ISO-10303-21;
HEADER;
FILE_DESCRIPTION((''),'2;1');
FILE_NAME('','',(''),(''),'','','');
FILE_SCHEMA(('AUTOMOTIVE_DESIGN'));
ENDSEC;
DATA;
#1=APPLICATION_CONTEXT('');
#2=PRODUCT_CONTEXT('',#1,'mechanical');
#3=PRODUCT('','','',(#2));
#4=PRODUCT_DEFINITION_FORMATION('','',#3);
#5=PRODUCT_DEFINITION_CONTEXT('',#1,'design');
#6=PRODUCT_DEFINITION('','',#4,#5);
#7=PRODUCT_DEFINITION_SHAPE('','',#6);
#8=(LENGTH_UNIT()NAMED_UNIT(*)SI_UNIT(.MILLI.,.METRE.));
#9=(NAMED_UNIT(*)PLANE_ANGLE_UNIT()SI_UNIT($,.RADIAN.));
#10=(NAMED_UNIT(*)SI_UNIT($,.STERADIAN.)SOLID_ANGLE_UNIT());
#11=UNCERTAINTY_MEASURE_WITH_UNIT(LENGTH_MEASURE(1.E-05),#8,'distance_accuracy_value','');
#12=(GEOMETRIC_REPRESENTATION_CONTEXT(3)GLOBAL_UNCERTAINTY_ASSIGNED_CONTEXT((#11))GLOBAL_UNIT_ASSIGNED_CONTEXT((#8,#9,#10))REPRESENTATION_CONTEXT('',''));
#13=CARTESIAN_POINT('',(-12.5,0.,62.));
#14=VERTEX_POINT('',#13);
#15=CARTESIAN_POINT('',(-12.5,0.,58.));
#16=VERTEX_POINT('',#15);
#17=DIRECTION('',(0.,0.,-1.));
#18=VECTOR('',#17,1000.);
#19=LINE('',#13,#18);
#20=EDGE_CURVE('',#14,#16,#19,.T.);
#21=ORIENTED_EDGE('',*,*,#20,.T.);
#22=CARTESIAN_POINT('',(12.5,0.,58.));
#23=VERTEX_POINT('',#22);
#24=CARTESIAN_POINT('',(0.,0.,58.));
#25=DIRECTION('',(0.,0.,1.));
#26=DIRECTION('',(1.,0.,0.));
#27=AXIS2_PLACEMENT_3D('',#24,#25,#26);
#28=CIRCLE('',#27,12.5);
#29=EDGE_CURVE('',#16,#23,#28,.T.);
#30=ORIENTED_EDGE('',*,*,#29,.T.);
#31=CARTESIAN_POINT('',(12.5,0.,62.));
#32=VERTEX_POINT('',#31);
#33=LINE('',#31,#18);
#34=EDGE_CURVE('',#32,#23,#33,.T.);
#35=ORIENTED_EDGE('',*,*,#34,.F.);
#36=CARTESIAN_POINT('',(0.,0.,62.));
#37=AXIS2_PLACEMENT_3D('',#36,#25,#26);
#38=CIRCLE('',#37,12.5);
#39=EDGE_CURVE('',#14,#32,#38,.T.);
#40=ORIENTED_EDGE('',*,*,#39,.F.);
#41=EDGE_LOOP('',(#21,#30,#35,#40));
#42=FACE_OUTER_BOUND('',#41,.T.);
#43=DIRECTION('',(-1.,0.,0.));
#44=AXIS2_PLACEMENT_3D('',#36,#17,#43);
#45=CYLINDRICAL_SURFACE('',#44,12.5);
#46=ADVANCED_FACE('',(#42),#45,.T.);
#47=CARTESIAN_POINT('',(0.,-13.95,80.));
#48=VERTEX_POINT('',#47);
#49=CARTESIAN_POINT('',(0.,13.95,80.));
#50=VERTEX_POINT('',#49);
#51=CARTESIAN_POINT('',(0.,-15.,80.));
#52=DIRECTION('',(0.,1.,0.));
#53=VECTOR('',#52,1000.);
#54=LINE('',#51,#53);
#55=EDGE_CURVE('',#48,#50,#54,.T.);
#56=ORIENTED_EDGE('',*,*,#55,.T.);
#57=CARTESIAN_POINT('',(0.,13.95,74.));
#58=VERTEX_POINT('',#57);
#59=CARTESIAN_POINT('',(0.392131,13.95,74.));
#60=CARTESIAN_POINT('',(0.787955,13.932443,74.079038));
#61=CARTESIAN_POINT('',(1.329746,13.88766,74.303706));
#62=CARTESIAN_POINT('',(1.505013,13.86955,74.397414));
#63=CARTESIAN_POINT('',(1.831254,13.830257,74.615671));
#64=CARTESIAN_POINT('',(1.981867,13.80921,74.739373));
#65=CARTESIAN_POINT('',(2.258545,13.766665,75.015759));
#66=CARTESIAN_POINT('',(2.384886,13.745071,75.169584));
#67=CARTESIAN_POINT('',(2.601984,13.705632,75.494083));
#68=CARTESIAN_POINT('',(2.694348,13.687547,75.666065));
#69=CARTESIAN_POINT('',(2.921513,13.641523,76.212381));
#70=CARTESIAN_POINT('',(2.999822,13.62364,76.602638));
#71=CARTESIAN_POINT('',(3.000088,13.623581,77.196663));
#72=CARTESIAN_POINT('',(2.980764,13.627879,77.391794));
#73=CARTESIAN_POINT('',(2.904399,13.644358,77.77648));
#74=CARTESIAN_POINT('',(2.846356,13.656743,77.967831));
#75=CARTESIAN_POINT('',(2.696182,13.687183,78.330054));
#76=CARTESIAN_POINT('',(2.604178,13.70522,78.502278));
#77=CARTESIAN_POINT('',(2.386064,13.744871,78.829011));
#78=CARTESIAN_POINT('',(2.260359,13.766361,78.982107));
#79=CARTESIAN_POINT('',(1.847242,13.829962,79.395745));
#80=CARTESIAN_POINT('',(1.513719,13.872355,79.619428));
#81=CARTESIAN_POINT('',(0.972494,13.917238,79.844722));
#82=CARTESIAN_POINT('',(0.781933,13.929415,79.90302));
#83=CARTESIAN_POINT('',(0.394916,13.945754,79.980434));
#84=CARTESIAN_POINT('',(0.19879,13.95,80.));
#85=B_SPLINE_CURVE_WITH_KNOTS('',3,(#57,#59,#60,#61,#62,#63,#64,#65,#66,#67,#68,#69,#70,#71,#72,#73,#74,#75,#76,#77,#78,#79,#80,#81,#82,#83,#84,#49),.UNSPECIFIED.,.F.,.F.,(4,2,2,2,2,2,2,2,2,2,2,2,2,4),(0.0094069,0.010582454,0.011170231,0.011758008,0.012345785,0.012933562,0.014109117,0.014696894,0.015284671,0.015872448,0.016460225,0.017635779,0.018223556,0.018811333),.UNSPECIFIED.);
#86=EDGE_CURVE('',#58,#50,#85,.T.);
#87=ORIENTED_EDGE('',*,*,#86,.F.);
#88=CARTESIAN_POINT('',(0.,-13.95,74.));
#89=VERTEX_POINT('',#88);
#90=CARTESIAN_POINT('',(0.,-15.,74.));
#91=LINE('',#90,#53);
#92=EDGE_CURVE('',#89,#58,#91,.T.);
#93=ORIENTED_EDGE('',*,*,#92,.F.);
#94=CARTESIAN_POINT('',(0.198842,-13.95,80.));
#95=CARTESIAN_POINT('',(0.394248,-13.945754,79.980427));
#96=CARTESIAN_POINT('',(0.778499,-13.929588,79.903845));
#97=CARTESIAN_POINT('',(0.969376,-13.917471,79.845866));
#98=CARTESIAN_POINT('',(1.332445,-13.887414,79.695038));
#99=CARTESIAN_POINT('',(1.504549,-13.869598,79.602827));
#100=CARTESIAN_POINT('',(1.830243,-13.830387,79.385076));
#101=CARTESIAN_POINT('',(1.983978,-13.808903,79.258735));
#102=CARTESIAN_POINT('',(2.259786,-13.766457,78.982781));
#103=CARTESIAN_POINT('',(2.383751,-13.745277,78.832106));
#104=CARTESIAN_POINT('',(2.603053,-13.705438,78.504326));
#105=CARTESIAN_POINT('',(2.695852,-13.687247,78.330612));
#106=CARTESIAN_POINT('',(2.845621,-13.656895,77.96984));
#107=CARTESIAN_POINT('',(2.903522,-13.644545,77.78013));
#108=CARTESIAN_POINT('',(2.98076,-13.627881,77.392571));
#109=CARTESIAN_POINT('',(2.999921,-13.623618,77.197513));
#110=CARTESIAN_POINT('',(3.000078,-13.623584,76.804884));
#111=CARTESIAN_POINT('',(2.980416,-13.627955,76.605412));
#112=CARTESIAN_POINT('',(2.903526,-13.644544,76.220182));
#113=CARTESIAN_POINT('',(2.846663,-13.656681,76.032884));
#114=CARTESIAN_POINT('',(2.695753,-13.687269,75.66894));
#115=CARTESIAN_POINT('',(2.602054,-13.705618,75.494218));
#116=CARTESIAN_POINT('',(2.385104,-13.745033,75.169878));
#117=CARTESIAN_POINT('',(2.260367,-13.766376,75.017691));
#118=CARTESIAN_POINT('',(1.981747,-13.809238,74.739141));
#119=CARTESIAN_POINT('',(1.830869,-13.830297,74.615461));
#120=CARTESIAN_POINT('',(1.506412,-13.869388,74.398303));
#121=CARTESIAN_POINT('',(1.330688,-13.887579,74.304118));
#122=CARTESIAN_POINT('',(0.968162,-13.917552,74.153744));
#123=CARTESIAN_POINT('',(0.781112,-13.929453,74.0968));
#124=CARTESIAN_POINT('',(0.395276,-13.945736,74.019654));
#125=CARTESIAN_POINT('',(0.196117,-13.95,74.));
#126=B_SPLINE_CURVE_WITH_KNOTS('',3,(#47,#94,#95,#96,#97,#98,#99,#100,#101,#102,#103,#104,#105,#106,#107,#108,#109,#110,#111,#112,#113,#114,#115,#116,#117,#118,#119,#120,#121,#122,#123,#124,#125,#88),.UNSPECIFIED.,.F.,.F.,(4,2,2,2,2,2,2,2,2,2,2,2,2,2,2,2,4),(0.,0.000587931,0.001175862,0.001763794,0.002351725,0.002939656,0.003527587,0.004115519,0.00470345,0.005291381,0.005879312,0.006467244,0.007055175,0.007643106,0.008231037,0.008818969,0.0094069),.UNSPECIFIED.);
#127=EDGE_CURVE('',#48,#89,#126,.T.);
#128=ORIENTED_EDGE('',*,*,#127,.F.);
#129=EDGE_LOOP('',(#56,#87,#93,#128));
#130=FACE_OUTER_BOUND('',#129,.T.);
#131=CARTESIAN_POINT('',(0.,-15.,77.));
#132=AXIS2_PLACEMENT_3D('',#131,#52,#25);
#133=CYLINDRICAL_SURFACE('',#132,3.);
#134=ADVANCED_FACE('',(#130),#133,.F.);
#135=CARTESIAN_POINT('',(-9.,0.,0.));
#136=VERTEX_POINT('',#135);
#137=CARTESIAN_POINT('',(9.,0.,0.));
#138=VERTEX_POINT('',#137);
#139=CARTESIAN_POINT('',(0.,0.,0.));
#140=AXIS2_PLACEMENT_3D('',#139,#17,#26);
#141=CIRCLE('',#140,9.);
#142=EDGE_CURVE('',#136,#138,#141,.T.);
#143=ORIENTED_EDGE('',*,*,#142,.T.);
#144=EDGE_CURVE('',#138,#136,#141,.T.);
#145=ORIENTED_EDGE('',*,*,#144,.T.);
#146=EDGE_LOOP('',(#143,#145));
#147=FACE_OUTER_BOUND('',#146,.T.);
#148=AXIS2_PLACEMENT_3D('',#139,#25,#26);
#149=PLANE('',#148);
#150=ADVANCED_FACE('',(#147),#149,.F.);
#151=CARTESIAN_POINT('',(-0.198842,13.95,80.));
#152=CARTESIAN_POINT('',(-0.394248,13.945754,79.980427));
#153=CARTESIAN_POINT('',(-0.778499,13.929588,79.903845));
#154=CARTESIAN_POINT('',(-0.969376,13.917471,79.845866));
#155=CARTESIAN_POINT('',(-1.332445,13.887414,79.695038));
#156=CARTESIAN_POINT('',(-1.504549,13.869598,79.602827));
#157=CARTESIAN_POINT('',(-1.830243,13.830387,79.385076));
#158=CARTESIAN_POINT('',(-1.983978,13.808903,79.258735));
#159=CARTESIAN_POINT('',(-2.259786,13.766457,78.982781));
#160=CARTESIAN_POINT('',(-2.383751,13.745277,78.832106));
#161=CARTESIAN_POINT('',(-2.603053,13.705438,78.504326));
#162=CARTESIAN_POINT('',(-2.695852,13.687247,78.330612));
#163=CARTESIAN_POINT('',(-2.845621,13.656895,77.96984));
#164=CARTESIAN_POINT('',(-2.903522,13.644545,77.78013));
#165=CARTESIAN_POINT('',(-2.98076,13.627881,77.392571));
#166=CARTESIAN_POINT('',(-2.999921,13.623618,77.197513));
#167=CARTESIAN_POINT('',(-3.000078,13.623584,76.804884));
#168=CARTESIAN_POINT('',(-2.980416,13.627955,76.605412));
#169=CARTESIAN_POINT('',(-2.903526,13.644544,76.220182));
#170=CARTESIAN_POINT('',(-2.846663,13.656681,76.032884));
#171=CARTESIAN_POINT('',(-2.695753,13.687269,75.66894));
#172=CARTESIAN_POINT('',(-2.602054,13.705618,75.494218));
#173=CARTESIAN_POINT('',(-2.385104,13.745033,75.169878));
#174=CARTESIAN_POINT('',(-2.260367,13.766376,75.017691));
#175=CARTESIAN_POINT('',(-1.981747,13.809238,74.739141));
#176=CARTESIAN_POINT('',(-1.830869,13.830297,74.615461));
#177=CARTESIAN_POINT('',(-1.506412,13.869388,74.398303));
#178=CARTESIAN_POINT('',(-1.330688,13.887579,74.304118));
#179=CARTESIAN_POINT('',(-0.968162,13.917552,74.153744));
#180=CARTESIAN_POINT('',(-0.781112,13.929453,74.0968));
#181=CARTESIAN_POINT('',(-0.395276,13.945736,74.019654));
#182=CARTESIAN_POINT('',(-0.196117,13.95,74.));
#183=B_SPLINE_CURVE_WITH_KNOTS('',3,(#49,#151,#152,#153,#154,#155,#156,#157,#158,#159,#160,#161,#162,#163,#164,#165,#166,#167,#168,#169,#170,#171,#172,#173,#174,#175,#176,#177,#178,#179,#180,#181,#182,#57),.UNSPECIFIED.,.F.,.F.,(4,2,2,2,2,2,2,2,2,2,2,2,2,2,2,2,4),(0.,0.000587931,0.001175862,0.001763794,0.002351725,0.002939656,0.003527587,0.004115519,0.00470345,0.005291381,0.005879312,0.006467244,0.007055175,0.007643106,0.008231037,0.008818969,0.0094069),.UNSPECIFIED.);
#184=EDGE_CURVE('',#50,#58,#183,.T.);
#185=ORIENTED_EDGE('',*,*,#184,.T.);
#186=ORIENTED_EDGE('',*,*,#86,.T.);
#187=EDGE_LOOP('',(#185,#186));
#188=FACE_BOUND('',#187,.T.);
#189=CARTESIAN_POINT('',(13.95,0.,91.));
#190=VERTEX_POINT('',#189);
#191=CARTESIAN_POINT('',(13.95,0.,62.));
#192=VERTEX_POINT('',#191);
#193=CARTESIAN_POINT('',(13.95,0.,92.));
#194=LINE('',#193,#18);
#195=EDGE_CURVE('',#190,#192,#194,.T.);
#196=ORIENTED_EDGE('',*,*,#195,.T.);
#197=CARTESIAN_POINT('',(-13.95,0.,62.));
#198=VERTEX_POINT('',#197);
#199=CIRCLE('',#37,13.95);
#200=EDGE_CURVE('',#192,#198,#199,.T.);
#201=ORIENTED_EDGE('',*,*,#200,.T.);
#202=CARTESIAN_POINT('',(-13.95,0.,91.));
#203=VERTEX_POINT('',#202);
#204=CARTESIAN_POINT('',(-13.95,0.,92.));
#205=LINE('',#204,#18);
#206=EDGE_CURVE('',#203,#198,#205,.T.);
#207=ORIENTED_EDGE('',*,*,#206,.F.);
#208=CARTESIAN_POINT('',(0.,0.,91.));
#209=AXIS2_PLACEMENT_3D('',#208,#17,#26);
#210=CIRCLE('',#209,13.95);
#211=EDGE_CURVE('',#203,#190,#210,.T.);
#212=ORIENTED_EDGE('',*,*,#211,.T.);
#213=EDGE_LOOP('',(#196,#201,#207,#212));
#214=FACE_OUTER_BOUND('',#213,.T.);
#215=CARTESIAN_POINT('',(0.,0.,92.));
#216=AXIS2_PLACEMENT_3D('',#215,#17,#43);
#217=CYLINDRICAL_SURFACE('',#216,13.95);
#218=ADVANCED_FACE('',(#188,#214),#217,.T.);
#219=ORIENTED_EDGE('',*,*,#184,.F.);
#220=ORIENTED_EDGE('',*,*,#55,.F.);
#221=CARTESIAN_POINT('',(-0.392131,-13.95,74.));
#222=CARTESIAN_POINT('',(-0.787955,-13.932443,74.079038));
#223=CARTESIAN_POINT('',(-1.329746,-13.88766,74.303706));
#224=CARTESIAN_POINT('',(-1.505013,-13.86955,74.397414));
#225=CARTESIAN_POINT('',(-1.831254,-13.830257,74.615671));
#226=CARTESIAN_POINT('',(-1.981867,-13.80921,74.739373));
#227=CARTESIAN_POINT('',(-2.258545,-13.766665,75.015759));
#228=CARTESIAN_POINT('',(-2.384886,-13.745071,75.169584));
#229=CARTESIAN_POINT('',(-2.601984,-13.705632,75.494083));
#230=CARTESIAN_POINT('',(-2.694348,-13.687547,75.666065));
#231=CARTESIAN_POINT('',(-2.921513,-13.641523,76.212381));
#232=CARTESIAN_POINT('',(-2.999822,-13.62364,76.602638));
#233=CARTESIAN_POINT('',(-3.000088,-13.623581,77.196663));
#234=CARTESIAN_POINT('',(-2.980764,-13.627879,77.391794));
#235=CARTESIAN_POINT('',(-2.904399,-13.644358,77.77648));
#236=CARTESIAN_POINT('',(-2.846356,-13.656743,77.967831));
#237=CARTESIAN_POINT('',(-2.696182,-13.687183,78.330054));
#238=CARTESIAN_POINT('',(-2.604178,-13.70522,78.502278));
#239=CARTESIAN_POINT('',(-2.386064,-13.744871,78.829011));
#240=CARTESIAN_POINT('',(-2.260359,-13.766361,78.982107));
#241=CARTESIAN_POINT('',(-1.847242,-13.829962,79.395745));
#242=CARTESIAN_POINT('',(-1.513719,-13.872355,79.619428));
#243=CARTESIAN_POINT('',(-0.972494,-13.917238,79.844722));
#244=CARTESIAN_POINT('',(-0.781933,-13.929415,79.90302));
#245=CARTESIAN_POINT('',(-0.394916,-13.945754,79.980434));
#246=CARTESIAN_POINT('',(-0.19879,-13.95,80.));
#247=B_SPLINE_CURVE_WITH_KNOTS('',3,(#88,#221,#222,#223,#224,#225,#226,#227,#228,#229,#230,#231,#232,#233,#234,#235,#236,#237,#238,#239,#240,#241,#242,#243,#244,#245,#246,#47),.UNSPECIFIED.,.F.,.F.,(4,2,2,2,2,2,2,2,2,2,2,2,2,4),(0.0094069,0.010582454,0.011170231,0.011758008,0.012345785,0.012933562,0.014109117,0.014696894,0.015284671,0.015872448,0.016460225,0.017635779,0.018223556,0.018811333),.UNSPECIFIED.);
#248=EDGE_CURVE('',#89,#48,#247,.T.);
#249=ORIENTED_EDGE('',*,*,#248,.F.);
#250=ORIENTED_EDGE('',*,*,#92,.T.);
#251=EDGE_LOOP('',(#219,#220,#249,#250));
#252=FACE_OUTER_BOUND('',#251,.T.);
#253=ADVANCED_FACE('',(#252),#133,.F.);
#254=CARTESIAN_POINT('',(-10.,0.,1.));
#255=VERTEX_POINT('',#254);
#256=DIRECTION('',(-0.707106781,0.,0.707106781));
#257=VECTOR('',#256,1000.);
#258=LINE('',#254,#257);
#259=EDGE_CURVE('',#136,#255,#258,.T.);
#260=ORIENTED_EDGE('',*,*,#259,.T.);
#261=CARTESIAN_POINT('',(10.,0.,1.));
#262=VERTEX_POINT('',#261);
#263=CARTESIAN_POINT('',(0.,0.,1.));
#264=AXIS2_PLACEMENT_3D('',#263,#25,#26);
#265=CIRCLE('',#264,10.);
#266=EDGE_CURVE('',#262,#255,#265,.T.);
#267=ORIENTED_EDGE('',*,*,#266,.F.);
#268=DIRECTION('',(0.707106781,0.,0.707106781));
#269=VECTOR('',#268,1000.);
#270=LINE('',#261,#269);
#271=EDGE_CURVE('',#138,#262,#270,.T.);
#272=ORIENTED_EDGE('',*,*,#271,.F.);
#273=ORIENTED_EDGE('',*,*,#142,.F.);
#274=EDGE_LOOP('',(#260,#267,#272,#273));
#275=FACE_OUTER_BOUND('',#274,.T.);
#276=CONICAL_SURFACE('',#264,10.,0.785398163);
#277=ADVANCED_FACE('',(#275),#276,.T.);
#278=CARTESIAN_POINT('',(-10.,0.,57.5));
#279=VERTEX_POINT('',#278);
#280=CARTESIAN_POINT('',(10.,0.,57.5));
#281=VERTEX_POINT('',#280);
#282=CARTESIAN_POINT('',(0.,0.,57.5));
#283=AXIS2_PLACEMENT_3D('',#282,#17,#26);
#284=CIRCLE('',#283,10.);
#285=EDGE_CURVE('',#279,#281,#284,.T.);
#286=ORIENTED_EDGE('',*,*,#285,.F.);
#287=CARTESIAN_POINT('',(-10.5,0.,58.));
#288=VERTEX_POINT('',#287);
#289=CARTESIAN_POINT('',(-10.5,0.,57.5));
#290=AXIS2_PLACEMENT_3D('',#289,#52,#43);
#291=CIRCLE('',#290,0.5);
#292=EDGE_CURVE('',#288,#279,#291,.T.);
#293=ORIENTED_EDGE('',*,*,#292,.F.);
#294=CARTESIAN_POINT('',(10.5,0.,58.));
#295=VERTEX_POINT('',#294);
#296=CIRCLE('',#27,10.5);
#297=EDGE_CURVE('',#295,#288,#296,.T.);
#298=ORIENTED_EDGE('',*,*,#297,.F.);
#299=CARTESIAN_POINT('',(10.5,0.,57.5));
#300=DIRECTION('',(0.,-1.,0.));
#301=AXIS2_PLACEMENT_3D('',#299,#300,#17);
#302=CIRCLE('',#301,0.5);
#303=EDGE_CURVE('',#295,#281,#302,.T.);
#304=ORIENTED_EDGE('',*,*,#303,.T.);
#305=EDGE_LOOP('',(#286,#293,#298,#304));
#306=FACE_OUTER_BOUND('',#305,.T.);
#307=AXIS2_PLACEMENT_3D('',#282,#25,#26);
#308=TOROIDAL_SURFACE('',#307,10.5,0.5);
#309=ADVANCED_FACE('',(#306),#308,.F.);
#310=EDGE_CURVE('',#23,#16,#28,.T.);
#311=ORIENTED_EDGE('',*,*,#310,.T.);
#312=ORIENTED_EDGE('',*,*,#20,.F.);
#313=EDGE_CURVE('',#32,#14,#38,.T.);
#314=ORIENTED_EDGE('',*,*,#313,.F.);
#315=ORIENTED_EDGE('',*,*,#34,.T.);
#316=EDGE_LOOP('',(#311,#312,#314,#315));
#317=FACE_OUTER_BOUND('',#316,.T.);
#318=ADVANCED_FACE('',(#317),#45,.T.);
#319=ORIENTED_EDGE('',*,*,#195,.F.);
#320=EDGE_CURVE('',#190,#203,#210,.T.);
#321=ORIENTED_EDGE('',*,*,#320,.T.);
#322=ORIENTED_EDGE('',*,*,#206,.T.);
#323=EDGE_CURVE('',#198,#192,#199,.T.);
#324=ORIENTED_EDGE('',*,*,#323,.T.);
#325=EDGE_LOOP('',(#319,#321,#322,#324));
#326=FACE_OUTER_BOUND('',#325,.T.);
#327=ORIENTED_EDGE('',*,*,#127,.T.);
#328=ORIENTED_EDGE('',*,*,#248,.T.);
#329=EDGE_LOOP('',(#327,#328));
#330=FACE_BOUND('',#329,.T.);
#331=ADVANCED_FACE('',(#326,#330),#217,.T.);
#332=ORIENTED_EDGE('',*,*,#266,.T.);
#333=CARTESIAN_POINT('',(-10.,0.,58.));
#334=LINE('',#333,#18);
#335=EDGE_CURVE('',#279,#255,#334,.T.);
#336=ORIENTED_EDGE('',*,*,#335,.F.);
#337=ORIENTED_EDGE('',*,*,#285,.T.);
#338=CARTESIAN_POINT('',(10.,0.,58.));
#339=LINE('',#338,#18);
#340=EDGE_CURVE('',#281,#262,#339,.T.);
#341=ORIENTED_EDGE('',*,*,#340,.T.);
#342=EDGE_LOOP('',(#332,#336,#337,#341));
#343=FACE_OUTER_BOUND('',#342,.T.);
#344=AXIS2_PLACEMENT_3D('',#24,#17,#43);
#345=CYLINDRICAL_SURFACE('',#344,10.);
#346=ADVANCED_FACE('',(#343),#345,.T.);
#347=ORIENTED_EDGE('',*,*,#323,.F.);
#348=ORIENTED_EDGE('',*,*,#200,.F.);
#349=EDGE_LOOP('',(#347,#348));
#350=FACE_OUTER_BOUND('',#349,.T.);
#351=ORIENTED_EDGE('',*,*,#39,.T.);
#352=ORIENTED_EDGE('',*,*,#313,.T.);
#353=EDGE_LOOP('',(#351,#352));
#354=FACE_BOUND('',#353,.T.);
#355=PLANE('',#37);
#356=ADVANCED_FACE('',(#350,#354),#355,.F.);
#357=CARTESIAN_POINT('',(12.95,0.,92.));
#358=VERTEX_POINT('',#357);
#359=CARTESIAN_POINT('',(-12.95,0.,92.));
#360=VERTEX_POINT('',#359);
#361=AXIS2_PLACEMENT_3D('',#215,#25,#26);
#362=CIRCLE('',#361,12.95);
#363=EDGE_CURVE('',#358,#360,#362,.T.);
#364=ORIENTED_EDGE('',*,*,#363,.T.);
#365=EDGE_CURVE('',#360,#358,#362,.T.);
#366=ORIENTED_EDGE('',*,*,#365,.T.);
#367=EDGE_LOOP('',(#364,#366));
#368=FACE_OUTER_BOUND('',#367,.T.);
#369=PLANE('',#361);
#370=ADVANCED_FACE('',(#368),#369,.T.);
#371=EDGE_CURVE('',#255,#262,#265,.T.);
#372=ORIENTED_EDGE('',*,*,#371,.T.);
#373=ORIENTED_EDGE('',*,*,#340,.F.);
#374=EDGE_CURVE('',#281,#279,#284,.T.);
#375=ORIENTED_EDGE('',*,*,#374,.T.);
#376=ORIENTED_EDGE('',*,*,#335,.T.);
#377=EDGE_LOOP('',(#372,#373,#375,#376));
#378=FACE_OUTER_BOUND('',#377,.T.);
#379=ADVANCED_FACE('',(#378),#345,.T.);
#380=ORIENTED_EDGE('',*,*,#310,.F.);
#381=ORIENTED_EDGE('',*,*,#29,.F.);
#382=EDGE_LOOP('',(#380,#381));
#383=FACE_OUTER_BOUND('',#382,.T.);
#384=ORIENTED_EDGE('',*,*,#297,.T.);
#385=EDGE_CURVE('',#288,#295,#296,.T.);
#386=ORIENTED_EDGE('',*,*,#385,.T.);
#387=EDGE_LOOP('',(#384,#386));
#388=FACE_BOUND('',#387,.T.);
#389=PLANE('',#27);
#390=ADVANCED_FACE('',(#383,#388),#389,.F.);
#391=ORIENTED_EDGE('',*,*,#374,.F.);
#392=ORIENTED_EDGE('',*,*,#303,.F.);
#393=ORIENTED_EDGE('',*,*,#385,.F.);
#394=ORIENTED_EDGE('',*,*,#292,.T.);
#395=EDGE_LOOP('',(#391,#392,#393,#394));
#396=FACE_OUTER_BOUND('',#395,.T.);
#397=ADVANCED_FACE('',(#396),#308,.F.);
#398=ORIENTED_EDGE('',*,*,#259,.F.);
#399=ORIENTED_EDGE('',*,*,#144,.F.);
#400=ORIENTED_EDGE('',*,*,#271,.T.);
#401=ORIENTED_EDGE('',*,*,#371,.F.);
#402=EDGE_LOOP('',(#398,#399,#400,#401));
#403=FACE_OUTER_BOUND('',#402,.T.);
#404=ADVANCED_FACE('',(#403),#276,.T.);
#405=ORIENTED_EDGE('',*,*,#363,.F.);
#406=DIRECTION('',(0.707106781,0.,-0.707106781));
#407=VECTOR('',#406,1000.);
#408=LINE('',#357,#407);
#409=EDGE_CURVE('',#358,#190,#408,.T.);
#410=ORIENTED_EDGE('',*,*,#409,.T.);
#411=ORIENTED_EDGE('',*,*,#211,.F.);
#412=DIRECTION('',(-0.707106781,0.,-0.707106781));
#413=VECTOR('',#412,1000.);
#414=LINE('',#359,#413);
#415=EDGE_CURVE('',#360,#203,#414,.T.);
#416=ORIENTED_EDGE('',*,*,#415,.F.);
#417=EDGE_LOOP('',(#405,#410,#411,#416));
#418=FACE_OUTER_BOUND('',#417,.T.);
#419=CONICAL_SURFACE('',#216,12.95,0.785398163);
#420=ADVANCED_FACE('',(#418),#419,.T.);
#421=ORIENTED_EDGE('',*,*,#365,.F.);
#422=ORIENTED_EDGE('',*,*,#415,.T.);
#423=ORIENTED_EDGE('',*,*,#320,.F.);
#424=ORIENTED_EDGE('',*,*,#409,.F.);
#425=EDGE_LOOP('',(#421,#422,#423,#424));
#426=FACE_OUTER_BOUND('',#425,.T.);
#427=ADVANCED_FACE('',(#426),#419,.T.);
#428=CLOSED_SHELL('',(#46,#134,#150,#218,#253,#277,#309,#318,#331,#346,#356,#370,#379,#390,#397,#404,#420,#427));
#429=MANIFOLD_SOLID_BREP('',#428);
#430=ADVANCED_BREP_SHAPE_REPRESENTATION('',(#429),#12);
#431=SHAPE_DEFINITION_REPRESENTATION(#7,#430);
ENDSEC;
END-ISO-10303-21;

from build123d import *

# Parameters (mm, degrees)
SKETCH_1_R          = 10
EXTRUDE_1_DEPTH     = 58
SKETCH_2_R          = 12.5
EXTRUDE_2_DEPTH     = 4
SKETCH_3_R          = 13.95
EXTRUDE_3_DEPTH     = 30
CHAMFER_1_SIZE      = 1
FILLET_1_R          = 0.5
SKETCH_4_R          = 3
CUT_EXTRUDE_1_DEPTH = 15


with BuildPart() as part:
    # 草图1 → 凸台-拉伸1 (new body)
    with BuildSketch(Plane.XY):
        with Locations(Location((0, 0, 0), (0, 0, 180))):
            Circle(SKETCH_1_R)
    extrude(amount=EXTRUDE_1_DEPTH)

    # 草图2 → 凸台-拉伸2 (add)
    with BuildSketch(Plane.XY.offset(58)):
        Circle(SKETCH_2_R)
    extrude(amount=EXTRUDE_2_DEPTH)

    # 草图3 → 凸台-拉伸3 (add)
    with BuildSketch(Plane.XY.offset(62)):
        Circle(SKETCH_3_R)
    extrude(amount=EXTRUDE_3_DEPTH)

    # 倒角1
    chamfer_1_edges = [part.edges().sort_by_distance(p)[0] for p in [
        (-13.95, 0, 92),
        (10, 0, 0),
    ]]
    chamfer(chamfer_1_edges, length=CHAMFER_1_SIZE)

    # 圆角1
    fillet_1_edges = [part.edges().sort_by_distance(p)[0] for p in [
        (10, 0, 58),
    ]]
    fillet(fillet_1_edges, radius=FILLET_1_R)

    # 草图4 → 切除-拉伸1 (cut, symmetric)
    with BuildSketch(Plane(origin=(0, 0, 0), x_dir=(1, 0, 0), z_dir=(0, 1, 0))):
        with Locations(Location((0, -77, 0), (0, 0, 270))):
            Circle(SKETCH_4_R)
    extrude(amount=CUT_EXTRUDE_1_DEPTH, both=True, mode=Mode.SUBTRACT)


solid = part.part
